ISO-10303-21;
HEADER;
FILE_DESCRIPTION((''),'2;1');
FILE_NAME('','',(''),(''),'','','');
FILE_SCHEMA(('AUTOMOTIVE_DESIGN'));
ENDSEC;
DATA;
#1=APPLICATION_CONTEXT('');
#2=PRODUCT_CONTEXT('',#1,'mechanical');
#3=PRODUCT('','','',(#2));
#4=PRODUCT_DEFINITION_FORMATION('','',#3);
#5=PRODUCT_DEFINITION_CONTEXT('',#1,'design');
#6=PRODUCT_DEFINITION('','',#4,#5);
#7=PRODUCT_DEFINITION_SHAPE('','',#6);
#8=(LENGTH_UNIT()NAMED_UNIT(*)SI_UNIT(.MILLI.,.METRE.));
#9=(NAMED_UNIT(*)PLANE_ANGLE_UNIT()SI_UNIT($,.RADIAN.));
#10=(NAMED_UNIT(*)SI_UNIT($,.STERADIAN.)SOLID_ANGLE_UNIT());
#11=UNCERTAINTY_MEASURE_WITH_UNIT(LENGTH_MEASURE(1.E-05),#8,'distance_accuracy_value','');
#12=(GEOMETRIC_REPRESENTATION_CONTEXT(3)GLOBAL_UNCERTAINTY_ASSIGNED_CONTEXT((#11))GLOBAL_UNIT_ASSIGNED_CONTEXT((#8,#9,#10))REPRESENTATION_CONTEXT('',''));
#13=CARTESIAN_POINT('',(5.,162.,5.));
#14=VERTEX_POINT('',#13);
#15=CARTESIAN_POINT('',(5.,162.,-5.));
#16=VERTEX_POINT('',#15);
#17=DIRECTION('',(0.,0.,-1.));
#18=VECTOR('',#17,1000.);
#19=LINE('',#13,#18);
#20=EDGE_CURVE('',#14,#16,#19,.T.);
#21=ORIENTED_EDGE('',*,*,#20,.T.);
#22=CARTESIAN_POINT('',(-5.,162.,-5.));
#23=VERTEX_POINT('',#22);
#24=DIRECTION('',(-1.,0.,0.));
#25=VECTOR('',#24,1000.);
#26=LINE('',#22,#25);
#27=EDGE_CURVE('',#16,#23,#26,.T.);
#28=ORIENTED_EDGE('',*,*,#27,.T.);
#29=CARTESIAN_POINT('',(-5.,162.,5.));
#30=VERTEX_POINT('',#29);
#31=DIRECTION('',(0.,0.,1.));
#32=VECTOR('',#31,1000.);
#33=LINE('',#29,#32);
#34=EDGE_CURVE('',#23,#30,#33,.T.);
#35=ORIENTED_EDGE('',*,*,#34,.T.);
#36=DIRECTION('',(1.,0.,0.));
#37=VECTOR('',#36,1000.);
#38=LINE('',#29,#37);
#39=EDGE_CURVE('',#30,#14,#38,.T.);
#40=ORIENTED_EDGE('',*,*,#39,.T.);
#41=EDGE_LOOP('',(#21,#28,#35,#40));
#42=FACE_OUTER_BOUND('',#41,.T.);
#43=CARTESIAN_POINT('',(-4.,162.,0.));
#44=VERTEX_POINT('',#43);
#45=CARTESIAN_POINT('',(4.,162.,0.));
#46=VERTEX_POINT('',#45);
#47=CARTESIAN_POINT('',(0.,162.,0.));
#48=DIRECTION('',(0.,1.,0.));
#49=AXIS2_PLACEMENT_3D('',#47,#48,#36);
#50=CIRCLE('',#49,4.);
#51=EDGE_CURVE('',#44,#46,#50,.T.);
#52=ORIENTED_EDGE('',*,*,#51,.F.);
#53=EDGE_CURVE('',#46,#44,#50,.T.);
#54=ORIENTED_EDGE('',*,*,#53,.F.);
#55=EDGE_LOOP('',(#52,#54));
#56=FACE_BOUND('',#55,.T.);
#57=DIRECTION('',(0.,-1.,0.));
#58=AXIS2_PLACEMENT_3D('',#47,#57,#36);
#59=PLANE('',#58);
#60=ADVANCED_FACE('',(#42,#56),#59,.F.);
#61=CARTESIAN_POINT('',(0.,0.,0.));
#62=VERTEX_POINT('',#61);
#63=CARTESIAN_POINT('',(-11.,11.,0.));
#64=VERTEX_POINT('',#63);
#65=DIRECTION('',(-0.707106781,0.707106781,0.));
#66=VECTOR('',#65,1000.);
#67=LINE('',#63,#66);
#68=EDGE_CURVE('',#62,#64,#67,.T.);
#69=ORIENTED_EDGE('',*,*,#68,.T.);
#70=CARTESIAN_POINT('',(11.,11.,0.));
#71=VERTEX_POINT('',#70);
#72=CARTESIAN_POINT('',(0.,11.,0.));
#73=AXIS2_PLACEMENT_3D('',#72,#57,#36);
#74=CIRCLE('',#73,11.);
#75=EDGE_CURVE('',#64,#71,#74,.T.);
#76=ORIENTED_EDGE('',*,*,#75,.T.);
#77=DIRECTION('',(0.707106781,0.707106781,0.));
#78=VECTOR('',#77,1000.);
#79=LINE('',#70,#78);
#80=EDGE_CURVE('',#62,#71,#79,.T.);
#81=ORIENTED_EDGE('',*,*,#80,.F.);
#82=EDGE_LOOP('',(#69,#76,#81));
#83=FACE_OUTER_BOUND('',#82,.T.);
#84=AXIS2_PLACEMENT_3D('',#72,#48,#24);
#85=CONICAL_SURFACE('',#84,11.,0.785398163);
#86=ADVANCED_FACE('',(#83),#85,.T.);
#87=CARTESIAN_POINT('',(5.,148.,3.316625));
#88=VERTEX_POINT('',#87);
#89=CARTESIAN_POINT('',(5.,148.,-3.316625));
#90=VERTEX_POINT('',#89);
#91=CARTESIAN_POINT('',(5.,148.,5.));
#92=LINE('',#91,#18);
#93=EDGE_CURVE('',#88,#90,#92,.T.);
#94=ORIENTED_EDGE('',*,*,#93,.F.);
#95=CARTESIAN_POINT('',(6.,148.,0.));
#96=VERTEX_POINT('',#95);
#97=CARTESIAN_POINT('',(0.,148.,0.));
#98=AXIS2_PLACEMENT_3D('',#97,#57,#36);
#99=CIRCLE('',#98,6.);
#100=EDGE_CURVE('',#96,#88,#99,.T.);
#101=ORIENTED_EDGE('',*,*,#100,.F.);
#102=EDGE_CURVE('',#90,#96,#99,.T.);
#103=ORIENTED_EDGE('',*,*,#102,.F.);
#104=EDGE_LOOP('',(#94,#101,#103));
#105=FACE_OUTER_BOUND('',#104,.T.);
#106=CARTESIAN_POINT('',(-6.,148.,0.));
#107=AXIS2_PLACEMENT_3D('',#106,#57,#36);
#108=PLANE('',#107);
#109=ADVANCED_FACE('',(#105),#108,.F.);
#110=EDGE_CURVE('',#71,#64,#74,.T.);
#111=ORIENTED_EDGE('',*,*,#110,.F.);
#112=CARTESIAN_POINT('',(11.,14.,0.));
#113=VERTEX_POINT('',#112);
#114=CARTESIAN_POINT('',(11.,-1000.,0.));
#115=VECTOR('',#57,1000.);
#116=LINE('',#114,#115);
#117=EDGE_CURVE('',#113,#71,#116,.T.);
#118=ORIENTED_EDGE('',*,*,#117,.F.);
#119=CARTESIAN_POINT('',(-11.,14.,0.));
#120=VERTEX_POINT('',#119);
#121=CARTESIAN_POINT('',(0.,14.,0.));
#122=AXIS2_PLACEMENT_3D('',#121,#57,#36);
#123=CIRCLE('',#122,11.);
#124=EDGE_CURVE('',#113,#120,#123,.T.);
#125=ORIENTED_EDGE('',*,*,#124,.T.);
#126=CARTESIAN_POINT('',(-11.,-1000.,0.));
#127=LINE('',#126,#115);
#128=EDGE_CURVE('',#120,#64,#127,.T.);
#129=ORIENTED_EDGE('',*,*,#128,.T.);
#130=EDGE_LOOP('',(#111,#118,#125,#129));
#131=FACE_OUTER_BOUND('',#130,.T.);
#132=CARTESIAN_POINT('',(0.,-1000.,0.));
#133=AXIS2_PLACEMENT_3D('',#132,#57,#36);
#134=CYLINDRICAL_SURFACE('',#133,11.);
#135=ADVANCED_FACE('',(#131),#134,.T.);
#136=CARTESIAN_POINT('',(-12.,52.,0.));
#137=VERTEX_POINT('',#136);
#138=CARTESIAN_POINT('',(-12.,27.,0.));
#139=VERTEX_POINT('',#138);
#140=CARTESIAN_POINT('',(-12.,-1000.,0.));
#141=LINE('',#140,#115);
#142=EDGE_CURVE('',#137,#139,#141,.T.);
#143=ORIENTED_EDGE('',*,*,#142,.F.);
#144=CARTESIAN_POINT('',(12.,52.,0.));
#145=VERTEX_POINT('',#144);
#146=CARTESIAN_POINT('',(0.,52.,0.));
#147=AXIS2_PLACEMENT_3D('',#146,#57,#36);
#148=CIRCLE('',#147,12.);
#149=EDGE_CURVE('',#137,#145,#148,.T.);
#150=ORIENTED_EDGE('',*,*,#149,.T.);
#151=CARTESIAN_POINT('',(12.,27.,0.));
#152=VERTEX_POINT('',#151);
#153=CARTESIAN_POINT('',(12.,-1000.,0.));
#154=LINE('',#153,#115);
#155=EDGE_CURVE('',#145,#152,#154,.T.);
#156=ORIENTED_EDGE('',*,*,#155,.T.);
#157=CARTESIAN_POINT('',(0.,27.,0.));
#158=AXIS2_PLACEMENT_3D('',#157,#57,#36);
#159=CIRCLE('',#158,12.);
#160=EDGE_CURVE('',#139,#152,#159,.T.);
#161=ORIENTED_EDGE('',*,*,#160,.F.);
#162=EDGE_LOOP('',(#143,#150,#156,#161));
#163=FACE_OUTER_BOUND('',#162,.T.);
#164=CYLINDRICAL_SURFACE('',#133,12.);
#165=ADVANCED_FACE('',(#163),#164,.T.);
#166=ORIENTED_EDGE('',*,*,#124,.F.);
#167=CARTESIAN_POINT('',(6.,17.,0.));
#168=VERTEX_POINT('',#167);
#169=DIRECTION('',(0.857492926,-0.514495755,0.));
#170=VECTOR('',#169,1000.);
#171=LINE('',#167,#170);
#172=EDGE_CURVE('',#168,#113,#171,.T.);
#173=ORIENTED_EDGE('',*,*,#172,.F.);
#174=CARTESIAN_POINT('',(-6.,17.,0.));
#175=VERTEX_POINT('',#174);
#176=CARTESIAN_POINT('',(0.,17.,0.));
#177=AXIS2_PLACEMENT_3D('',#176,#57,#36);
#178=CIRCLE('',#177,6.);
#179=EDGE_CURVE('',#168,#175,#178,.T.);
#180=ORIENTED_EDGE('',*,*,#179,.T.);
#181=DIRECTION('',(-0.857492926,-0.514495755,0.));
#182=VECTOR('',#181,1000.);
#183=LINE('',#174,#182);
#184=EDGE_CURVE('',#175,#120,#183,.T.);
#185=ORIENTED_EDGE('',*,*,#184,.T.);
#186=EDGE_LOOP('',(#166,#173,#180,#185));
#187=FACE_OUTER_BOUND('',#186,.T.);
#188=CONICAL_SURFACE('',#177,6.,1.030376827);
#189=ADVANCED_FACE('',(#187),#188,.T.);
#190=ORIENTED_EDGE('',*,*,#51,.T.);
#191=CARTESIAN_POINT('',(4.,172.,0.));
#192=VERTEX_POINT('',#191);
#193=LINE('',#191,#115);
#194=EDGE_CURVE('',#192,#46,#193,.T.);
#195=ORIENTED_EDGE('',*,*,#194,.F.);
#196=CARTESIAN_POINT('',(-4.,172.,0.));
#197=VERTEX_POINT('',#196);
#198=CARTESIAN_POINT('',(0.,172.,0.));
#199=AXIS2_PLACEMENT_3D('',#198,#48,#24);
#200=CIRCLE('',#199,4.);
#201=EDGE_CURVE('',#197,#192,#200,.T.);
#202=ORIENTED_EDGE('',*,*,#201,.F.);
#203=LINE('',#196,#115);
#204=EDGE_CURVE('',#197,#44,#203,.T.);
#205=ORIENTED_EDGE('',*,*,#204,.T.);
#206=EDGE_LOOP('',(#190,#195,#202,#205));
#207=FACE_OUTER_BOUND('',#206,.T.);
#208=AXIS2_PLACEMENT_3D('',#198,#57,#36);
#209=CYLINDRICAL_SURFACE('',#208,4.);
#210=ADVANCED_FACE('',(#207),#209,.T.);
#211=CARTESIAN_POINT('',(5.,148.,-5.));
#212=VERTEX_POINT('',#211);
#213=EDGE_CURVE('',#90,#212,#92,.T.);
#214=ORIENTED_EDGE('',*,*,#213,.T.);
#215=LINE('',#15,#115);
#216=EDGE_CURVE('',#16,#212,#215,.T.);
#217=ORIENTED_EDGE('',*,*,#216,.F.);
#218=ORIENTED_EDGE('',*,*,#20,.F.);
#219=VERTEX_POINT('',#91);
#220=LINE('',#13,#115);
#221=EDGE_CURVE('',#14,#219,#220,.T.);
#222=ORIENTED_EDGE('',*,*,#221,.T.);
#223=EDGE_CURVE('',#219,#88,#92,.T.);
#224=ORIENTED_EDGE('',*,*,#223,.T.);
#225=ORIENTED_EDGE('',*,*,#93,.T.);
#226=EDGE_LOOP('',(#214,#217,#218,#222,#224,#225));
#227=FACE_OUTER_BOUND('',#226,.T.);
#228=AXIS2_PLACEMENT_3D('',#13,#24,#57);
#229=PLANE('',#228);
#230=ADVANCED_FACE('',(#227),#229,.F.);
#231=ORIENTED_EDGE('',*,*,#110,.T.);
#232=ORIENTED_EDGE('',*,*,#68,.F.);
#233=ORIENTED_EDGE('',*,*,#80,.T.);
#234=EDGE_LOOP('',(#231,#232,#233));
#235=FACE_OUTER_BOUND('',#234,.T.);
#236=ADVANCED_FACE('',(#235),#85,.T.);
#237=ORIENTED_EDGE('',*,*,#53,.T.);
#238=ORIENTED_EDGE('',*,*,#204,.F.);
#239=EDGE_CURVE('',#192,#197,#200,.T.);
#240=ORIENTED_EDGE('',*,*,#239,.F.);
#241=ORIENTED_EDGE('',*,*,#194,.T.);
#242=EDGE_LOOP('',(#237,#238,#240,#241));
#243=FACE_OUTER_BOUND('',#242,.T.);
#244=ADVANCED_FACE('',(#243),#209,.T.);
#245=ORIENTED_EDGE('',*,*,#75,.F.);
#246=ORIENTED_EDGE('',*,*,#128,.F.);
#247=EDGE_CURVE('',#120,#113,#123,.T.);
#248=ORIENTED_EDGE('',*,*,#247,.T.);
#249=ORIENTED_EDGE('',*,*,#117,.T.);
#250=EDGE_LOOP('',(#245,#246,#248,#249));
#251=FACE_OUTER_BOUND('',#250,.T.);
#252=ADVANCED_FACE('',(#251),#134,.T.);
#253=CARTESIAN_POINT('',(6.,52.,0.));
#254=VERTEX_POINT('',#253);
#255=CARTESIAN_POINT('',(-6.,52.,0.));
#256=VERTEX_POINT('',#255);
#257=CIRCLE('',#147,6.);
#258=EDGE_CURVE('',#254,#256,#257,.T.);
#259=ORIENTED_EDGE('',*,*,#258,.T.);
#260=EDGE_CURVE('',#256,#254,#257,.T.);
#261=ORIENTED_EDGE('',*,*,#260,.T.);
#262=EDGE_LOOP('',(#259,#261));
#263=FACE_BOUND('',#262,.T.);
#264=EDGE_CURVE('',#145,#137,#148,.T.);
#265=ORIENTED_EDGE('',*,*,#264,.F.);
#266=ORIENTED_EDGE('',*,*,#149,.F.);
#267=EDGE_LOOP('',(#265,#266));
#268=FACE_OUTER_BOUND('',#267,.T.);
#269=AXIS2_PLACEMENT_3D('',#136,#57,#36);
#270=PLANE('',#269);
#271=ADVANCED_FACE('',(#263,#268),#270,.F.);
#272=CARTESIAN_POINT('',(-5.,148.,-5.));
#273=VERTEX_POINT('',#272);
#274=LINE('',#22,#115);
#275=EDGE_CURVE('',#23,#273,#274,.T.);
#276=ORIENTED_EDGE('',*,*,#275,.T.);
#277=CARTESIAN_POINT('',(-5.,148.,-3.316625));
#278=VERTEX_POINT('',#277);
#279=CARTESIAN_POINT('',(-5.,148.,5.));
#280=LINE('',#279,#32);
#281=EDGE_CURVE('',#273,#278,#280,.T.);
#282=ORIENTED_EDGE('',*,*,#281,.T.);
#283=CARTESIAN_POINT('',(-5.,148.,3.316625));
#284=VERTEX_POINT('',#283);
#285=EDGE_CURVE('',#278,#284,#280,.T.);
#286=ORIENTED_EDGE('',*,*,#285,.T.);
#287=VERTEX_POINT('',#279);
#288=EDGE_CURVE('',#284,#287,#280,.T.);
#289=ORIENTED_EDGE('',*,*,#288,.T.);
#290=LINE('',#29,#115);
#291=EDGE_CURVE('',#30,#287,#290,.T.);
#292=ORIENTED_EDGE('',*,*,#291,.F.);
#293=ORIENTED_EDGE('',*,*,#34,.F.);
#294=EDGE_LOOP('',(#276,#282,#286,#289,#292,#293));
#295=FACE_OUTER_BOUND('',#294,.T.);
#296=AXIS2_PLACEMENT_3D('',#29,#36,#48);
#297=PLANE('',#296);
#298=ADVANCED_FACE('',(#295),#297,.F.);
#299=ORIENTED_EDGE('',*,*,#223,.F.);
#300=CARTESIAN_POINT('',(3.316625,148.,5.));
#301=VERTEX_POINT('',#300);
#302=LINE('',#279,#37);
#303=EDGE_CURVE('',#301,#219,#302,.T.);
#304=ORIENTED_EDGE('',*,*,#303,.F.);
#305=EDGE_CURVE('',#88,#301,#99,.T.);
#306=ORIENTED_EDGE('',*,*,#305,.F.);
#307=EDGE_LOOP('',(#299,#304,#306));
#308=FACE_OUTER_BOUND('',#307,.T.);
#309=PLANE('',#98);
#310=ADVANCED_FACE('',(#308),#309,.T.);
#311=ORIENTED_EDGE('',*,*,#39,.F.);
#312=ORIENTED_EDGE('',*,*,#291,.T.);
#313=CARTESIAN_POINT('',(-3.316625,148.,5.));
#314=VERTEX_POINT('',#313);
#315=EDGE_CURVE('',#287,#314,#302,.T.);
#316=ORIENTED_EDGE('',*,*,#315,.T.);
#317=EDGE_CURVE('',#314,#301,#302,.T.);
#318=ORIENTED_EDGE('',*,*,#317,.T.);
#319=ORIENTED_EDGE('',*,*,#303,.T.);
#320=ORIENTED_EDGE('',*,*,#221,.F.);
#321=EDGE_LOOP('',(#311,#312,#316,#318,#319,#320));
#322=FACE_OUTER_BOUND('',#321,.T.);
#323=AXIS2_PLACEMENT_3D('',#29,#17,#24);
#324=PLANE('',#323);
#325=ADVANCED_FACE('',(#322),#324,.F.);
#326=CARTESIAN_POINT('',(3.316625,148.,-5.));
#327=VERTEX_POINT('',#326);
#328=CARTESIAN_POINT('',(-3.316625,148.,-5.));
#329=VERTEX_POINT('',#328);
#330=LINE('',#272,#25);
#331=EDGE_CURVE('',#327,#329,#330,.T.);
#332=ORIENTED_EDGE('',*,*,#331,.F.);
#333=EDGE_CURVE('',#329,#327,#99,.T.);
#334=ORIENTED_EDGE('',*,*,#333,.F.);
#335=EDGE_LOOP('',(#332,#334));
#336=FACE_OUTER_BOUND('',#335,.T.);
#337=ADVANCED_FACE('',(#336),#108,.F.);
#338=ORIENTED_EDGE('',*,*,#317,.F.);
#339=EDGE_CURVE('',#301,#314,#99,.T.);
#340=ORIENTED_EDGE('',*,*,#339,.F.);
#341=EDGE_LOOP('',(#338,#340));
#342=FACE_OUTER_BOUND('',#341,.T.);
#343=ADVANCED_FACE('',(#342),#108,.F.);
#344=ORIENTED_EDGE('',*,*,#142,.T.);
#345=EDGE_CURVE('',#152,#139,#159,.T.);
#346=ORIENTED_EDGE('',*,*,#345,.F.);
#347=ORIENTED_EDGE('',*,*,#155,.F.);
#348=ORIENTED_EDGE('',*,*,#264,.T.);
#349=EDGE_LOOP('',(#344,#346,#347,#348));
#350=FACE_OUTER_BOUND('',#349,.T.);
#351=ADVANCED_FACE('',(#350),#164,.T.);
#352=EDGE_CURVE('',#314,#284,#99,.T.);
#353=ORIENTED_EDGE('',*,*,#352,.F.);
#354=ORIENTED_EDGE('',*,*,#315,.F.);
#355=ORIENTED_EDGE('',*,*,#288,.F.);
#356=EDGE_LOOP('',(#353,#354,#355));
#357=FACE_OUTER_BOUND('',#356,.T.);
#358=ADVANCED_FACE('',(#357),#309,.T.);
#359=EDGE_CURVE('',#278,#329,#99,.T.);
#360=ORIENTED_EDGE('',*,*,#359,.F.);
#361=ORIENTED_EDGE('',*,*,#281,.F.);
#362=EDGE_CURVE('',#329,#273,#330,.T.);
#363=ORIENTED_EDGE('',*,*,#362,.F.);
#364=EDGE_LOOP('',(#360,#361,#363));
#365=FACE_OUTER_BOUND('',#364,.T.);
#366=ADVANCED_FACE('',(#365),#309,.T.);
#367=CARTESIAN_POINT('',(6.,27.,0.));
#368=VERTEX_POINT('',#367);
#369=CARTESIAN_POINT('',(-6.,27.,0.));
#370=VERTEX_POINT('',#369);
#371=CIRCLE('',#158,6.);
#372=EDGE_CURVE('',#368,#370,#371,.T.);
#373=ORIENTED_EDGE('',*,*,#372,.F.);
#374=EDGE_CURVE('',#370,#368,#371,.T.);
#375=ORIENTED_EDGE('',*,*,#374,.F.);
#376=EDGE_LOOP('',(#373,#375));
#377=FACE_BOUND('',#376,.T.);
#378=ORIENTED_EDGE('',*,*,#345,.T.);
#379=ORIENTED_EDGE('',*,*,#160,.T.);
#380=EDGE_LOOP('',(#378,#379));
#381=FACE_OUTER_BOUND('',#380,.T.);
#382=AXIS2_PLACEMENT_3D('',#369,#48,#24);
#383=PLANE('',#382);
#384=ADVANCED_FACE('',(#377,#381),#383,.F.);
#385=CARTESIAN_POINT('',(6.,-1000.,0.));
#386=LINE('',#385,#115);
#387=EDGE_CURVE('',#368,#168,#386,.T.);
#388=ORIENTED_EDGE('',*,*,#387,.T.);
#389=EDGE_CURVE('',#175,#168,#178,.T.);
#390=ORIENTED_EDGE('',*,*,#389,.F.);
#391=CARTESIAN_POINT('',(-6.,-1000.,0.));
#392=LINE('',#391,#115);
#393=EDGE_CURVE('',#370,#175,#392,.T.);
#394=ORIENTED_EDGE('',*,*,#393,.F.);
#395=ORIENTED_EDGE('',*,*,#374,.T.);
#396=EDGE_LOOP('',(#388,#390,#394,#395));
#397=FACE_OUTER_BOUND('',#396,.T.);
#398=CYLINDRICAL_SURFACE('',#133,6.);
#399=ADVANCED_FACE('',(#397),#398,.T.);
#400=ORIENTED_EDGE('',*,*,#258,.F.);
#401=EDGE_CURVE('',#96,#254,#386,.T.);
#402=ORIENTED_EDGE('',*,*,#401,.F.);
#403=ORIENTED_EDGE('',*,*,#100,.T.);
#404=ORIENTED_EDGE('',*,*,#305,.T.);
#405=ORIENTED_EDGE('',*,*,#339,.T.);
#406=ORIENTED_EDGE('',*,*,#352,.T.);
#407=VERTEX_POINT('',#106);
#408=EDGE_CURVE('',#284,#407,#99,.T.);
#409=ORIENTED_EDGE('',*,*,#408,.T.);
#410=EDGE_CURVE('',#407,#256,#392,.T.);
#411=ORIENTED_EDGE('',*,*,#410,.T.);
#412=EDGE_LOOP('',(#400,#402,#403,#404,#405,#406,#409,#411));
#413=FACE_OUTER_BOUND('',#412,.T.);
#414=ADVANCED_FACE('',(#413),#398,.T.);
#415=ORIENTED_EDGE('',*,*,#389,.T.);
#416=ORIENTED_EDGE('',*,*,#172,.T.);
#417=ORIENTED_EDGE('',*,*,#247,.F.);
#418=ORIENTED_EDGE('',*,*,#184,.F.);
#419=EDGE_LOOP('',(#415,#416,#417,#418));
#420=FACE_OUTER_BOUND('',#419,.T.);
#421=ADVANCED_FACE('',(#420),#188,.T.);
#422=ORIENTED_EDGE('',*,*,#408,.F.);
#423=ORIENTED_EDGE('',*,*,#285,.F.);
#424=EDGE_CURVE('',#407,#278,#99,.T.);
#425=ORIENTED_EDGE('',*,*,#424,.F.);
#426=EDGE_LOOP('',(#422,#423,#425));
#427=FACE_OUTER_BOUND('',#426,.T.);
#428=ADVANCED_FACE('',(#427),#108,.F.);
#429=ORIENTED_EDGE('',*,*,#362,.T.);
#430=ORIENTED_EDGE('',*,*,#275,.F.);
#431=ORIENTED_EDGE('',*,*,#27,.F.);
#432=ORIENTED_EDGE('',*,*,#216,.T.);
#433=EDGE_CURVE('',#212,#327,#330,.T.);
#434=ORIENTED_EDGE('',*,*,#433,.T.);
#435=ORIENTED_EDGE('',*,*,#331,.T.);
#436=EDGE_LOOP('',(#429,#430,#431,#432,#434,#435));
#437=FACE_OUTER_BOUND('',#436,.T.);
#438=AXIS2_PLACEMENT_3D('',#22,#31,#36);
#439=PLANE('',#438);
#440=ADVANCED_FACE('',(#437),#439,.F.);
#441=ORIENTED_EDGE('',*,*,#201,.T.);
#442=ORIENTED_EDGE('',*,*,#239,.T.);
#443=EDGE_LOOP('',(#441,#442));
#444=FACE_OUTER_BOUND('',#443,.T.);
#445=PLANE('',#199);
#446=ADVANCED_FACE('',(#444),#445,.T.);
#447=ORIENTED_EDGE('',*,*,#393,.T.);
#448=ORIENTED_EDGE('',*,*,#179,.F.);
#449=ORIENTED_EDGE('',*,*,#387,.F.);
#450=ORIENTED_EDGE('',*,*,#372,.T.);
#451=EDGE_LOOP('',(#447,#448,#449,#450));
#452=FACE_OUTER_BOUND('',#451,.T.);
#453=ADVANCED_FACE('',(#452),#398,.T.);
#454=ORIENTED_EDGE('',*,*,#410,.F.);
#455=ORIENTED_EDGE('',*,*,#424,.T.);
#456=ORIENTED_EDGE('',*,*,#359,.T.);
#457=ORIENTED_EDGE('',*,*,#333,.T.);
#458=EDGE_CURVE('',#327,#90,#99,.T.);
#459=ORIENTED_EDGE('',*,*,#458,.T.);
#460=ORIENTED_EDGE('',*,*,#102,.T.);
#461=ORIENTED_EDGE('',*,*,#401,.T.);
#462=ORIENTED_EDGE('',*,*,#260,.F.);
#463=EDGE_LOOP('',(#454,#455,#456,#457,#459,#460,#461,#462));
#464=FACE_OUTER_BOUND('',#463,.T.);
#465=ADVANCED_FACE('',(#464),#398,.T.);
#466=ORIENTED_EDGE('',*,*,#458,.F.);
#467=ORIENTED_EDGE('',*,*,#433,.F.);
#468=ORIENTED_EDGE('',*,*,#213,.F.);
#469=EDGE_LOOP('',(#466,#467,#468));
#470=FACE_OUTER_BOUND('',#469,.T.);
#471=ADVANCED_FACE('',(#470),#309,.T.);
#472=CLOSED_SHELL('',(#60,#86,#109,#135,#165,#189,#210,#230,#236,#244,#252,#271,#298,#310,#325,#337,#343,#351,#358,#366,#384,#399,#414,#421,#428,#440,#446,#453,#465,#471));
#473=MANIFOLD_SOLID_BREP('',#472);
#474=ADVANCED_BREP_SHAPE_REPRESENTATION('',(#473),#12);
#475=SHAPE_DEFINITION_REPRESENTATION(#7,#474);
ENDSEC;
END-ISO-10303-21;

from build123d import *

# Parameters (mm, degrees)
SKETCH2_W           = 10
SKETCH2_H           = 10
BOSS_EXTRUDE1_DEPTH = 14
SKETCH3_R           = 4
BOSS_EXTRUDE2_DEPTH = 10


with BuildPart() as part:
    # Sketch1 → Revolve1 (revolve)
    with BuildSketch(Plane.XY, mode=Mode.PRIVATE) as revolve1_sk:
        Polygon((0, 0), (-11, 11), (-11, 14), (-6, 17), (-6, 27), (-12, 27), (-12, 52), (-6, 52), (-6, 148), (0, 148), align=None)
    revolve(revolve1_sk.sketch.rotate(Axis((0, -1000, 0), (0, 1, 0)), 180), axis=Axis((0, -1000, 0), (0, 1, 0)))

    # Sketch2 → Boss-Extrude1 (add)
    with BuildSketch(Plane(origin=(0, 148, 0), x_dir=(1, 0, 0), z_dir=(0, 1, 0))):
        Rectangle(SKETCH2_W, SKETCH2_H)
    extrude(amount=BOSS_EXTRUDE1_DEPTH)

    # Sketch3 → Boss-Extrude2 (add)
    with BuildSketch(Plane(origin=(0, 162, 0), x_dir=(1, 0, 0), z_dir=(0, 1, 0))):
        Circle(SKETCH3_R)
    extrude(amount=BOSS_EXTRUDE2_DEPTH)


solid = part.part
